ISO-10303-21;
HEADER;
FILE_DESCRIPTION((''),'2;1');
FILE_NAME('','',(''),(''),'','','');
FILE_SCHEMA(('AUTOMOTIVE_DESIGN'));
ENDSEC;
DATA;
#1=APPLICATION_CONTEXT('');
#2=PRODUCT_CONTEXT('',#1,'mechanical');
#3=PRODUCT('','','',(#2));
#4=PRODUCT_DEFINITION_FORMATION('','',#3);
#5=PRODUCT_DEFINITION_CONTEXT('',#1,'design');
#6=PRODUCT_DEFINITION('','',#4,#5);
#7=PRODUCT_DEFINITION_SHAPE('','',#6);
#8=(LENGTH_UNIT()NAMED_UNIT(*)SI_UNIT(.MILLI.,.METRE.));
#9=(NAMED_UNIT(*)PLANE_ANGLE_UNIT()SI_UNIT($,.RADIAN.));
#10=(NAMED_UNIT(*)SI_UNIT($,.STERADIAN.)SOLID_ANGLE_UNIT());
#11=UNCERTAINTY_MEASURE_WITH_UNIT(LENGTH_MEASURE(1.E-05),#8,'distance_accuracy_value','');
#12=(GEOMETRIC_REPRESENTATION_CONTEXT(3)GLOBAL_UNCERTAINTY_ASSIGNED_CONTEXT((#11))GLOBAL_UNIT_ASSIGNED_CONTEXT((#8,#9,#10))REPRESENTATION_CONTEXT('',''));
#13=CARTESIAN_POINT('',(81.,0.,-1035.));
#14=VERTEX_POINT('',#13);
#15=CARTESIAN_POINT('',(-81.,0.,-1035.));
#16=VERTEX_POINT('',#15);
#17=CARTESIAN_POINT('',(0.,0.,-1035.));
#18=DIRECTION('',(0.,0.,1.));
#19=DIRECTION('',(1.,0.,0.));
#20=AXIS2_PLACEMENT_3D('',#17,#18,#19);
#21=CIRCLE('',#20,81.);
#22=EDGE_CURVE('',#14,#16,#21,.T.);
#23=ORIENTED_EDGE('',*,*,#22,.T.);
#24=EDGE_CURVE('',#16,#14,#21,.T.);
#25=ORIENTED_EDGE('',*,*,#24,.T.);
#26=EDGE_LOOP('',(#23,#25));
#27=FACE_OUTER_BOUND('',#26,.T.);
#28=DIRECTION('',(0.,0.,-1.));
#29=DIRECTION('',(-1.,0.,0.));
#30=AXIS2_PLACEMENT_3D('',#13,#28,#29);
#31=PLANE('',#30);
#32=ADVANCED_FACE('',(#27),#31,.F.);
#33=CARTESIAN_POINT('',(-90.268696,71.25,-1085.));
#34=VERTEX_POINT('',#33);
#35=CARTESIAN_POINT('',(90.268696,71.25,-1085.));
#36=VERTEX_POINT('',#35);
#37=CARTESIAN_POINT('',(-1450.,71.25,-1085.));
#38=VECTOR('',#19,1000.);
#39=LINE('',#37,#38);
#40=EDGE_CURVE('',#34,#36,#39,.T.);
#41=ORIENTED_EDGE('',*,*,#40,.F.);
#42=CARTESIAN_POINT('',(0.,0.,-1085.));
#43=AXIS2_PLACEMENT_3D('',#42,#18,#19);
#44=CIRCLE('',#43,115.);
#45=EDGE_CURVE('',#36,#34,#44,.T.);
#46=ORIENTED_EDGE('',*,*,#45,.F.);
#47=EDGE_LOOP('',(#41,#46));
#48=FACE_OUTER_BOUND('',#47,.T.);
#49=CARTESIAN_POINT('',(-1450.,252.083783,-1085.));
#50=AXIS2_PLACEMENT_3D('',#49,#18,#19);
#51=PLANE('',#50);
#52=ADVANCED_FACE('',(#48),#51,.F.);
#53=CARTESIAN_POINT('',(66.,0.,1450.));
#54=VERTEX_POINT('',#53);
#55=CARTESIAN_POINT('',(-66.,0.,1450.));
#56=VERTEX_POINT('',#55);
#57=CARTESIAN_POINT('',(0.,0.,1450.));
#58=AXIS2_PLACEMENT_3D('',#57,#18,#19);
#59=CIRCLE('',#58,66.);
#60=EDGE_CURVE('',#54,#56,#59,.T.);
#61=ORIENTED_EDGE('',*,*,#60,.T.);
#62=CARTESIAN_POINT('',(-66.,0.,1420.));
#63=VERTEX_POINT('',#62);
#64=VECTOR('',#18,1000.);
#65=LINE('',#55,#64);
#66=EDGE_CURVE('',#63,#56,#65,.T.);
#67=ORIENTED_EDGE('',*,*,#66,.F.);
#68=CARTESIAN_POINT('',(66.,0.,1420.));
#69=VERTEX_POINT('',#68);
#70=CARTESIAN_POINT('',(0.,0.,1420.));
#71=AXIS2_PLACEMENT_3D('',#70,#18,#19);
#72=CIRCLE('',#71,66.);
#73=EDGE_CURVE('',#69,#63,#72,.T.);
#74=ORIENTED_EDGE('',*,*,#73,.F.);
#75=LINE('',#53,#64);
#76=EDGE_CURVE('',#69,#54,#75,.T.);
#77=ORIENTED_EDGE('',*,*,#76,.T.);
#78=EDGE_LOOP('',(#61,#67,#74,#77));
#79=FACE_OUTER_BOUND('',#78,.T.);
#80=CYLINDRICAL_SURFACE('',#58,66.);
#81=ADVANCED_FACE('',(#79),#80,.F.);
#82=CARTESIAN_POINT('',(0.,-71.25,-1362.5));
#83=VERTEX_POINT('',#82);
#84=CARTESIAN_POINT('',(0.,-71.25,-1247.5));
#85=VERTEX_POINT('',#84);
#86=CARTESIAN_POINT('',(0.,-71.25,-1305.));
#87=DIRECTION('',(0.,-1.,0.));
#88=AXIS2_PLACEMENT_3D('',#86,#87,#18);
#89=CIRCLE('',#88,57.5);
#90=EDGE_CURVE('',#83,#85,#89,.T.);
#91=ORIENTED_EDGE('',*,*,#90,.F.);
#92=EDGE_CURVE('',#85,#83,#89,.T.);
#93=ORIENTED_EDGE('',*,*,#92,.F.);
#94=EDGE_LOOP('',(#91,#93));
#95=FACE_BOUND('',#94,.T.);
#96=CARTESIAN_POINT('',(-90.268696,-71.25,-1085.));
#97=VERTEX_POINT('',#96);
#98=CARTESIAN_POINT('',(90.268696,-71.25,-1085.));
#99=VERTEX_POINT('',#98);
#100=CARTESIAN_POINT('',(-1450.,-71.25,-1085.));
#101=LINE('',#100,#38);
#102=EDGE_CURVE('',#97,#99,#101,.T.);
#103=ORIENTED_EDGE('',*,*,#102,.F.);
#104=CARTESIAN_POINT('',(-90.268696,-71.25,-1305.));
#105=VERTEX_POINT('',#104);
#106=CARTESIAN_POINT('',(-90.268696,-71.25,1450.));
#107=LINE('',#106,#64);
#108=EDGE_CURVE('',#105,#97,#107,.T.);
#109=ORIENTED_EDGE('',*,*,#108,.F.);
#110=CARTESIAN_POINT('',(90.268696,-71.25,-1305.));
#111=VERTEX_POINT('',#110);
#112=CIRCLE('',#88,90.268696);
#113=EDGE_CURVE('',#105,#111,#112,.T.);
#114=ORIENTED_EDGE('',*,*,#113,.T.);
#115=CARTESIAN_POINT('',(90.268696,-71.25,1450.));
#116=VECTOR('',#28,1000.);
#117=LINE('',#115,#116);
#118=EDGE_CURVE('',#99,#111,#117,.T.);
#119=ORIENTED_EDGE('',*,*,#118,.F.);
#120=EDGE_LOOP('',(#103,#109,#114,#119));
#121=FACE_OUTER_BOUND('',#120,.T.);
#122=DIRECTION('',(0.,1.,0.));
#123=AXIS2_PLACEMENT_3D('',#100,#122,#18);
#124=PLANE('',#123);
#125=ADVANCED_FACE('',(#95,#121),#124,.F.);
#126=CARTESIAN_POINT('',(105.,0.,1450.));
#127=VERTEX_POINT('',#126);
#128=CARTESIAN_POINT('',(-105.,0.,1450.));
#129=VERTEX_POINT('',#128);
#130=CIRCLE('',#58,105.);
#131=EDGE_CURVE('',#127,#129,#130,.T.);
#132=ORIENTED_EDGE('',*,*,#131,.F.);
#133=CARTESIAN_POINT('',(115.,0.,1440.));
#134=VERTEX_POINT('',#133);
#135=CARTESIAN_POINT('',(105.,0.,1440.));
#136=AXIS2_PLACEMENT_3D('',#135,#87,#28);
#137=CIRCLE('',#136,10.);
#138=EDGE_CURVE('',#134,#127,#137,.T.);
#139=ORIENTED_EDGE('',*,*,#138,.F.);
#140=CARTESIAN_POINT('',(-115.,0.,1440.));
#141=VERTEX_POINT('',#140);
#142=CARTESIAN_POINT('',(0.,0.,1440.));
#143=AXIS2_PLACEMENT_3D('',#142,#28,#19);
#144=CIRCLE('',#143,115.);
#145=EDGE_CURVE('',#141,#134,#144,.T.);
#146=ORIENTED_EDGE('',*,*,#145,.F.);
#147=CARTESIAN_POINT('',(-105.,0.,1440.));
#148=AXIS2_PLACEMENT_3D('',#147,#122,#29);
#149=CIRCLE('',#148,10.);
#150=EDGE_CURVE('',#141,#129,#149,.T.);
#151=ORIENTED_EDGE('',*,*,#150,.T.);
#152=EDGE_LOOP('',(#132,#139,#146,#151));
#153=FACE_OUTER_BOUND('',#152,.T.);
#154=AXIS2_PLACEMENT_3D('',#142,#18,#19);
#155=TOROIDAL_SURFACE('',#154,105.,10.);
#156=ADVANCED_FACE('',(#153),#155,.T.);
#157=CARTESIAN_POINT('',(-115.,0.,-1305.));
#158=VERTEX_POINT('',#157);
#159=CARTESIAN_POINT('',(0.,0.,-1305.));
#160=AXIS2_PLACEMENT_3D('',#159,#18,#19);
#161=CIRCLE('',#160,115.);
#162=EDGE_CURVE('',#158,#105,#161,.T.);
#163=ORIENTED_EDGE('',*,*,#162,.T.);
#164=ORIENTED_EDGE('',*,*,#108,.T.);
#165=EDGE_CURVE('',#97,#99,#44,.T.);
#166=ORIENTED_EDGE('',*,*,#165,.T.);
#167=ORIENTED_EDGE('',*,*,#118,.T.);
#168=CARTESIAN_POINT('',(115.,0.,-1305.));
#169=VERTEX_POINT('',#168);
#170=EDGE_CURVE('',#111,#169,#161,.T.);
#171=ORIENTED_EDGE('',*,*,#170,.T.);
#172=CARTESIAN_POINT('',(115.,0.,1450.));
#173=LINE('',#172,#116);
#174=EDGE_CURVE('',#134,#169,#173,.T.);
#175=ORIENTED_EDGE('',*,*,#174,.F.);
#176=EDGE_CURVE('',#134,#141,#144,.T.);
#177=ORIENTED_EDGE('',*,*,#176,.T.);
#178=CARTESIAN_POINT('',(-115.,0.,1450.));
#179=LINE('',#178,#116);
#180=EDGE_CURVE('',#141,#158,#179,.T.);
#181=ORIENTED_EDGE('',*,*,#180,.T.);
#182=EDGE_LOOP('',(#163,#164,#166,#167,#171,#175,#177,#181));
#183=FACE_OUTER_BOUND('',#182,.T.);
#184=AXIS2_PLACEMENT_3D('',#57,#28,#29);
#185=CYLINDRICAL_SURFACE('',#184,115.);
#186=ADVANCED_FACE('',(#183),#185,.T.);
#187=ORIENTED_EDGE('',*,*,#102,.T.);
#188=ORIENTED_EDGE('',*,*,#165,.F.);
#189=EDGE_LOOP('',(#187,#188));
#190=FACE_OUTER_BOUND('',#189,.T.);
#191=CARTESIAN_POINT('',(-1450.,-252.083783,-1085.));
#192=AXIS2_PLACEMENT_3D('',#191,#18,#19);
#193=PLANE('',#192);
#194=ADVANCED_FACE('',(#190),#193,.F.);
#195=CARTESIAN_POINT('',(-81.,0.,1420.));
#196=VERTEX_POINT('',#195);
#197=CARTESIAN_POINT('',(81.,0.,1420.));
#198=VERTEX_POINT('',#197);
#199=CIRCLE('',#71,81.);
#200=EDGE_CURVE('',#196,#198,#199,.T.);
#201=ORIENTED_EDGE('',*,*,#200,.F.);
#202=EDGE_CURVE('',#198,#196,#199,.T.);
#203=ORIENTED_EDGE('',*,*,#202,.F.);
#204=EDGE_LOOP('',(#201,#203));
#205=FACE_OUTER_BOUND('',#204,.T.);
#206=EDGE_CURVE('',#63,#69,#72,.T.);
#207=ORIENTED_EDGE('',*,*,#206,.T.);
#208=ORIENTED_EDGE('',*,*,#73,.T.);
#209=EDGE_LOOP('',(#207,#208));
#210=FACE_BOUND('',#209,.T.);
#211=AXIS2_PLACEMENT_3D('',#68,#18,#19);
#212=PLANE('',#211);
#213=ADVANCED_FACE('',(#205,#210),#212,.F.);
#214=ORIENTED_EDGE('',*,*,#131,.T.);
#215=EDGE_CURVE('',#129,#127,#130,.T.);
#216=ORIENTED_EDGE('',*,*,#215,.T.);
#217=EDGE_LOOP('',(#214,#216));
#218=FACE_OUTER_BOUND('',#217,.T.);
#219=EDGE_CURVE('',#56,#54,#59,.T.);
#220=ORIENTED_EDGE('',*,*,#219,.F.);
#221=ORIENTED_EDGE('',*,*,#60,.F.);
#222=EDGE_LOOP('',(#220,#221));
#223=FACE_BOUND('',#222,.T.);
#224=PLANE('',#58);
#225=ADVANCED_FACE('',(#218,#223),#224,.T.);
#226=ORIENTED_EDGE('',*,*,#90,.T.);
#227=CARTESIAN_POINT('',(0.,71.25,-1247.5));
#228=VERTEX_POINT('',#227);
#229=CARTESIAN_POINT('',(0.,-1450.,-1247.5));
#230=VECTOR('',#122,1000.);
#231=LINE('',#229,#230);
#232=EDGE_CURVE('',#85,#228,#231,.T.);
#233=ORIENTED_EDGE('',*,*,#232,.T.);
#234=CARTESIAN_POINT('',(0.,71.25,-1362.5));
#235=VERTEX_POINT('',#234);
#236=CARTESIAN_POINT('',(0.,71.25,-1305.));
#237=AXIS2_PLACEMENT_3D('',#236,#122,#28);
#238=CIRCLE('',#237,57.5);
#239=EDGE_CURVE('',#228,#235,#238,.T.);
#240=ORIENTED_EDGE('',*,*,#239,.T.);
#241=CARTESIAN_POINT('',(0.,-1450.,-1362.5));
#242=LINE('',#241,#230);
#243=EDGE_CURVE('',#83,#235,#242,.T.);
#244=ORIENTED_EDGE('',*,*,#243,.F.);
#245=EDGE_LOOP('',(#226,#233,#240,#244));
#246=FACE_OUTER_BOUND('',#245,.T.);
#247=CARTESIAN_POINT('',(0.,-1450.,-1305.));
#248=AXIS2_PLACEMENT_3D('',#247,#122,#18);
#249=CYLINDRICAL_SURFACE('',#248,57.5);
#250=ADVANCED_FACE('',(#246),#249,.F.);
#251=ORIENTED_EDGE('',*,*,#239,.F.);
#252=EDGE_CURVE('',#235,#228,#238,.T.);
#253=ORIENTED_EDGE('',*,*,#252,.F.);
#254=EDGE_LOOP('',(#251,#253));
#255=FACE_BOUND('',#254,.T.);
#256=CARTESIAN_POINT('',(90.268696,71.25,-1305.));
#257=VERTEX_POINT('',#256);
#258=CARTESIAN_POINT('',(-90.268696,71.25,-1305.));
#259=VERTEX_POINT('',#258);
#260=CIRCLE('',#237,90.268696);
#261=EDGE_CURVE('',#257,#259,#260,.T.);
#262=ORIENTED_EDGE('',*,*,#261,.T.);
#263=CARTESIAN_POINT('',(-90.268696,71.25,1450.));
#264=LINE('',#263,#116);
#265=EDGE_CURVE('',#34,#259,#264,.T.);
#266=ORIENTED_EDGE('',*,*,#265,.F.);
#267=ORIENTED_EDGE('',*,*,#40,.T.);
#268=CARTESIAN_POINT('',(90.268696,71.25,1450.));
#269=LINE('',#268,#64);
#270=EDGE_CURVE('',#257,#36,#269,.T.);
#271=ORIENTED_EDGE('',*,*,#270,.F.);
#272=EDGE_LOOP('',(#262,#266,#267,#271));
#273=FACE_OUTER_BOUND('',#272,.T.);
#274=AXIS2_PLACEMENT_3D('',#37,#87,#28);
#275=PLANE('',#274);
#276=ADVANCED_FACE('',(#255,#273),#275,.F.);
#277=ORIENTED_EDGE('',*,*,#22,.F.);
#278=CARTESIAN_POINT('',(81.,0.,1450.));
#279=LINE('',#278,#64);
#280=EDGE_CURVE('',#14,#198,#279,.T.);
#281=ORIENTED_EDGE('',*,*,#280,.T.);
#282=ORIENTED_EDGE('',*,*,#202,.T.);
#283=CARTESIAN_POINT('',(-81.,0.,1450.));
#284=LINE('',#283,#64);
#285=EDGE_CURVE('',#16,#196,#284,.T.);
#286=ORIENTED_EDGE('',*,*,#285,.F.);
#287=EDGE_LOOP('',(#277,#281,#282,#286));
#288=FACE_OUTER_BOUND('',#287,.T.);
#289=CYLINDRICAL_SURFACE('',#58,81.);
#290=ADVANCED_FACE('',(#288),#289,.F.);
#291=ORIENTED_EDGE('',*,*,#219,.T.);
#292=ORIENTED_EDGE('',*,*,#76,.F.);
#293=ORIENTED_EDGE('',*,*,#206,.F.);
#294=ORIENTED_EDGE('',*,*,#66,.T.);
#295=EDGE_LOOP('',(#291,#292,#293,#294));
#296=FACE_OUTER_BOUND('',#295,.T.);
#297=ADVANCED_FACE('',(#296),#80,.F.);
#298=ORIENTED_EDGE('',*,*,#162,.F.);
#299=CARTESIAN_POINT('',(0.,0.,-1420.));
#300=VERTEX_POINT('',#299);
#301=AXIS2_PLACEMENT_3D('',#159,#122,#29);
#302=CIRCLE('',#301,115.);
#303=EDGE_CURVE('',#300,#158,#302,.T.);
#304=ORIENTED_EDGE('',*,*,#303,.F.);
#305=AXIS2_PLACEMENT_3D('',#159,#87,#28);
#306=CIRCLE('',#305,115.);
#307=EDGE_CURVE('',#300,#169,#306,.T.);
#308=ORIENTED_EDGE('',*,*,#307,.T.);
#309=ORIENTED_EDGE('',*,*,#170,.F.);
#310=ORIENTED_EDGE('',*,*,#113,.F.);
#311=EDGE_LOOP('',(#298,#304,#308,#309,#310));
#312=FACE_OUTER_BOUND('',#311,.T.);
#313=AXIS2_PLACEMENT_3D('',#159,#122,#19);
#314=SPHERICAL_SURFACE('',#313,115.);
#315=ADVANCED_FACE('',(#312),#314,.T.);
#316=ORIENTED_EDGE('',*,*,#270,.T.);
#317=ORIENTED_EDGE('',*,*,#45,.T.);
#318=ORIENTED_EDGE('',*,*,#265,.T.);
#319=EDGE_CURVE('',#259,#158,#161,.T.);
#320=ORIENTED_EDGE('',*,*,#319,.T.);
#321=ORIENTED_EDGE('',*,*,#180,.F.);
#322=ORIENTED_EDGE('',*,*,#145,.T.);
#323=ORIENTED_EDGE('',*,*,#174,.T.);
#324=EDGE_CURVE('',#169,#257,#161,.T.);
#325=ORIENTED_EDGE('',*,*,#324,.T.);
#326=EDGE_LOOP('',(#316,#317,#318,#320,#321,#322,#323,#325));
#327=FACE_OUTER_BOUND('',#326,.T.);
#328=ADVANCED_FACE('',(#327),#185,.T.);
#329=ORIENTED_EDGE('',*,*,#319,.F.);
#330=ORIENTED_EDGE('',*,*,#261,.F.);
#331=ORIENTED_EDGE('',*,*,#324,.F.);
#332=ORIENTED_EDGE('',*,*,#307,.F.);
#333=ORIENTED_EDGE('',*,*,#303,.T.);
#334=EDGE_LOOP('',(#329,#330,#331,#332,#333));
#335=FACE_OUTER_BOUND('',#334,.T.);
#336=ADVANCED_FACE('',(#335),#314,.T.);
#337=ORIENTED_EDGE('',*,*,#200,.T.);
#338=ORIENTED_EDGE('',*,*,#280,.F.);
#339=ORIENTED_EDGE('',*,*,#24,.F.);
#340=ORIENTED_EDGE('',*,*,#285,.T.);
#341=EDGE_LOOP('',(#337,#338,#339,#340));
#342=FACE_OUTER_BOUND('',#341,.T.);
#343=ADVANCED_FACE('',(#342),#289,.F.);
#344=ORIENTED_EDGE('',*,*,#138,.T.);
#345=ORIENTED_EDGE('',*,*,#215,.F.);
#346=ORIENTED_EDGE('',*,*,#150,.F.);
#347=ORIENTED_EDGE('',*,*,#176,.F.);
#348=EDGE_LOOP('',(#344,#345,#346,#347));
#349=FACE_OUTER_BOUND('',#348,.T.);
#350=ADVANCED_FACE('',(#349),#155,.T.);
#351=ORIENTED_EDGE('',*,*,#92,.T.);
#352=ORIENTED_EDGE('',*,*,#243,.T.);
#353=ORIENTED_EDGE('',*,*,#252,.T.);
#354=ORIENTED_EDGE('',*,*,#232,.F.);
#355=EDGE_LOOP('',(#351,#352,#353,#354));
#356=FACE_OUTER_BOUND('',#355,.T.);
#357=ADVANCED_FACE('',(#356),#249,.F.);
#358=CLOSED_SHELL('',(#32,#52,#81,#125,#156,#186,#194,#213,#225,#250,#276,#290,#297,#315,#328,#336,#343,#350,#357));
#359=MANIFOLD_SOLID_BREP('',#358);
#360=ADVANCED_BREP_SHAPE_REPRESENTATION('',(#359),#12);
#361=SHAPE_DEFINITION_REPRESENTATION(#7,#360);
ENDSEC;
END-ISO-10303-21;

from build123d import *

# Parameters (mm, degrees)
BARREL_PROFILE_230_SKETCH_R  = 115
BARREL_BODY_230X2900_DEPTH   = 1450
END_TRIM_CUT_SKETCH_R        = 57.49999999999997
END_TRIM_CUT_DEPTH           = 1450
CLEVIS_EYE_PROFILE_SKETCH_W  = 365
CLEVIS_EYE_PROFILE_SKETCH_H  = 180.83378269641366
CLEVIS_EYE_PROFILE_CUT_DEPTH = 1450
EDGE_FILLET_R10_R            = 10


with BuildPart() as part:
    # Barrel Profile Ø230 Sketch → Barrel Body Ø230x2900 (new, symmetric)
    with BuildSketch(Plane.XY):
        Circle(BARREL_PROFILE_230_SKETCH_R)
    extrude(amount=BARREL_BODY_230X2900_DEPTH, both=True)

    # End Trim Cut Sketch → End Trim Cut (cut, symmetric)
    with BuildSketch(Plane(origin=(0, 0, 0), x_dir=(1, 0, 0), z_dir=(0, 1, 0))):
        with Locations(Location((0, 1305, 0), (0, 0, 270))):
            Circle(END_TRIM_CUT_SKETCH_R)
    extrude(amount=END_TRIM_CUT_DEPTH, both=True, mode=Mode.SUBTRACT)

    # Clevis Eye Profile Sketch → Clevis Eye Profile Cut (cut, symmetric)
    with BuildSketch(Plane(origin=(0, 0, 0), x_dir=(0, 0, -1), z_dir=(1, 0, 0))):
        with Locations((1267.5, -161.66689134820675)):
            Rectangle(CLEVIS_EYE_PROFILE_SKETCH_W, CLEVIS_EYE_PROFILE_SKETCH_H)
        with Locations((1267.5, 161.66689134820675)):
            Rectangle(CLEVIS_EYE_PROFILE_SKETCH_W, CLEVIS_EYE_PROFILE_SKETCH_H)
    extrude(amount=CLEVIS_EYE_PROFILE_CUT_DEPTH, both=True, mode=Mode.SUBTRACT)

    # Bore End Revolve Sketch → Bore End Revolved Cut (revolve, cut)
    with BuildSketch(Plane(origin=(0, 0, 0), x_dir=(1, 0, 0), z_dir=(0, 1, 0)), mode=Mode.PRIVATE) as bore_end_revolved_cut_sk:
        with BuildLine():
            Line((0, 1537.1393692003157), (209.05243850437193, 1537.1393692003157))
            Line((209.05243850437193, 1537.1393692003157), (209.05243850437193, 1305))
            Line((209.05243850437193, 1305), (115, 1305))
            ThreePointArc((115, 1305), (81.31727983645297, 1386.317279836453), (0, 1420))
            Line((0, 1420), (0, 1537.1393692003157))
        make_face()
    revolve(bore_end_revolved_cut_sk.sketch.rotate(Axis((0, 0, -1420), (0, 0, -1)), 218.284391292), axis=Axis((0, 0, -1420), (0, 0, -1)), mode=Mode.SUBTRACT)

    # Eye End Revolve Sketch → Eye End Revolved Cut (revolve, cut)
    with BuildSketch(Plane(origin=(0, 0, 0), x_dir=(1, 0, 0), z_dir=(0, 1, 0))):
        Polygon((0, -1450), (-6.94e-15, 1034.9999999999995), (81, 1035), (81, -1420), (66, -1420), (66, -1450), align=None)
    revolve(axis=Axis((0, 0, 1450), (0, 0, -1)), mode=Mode.SUBTRACT)

    # Edge Fillet R10
    edge_fillet_r10_edges = [part.edges().sort_by_distance(p)[0] for p in [
        (-115, 1.408e-14, 1450),
    ]]
    fillet(edge_fillet_r10_edges, radius=EDGE_FILLET_R10_R)


solid = part.part
